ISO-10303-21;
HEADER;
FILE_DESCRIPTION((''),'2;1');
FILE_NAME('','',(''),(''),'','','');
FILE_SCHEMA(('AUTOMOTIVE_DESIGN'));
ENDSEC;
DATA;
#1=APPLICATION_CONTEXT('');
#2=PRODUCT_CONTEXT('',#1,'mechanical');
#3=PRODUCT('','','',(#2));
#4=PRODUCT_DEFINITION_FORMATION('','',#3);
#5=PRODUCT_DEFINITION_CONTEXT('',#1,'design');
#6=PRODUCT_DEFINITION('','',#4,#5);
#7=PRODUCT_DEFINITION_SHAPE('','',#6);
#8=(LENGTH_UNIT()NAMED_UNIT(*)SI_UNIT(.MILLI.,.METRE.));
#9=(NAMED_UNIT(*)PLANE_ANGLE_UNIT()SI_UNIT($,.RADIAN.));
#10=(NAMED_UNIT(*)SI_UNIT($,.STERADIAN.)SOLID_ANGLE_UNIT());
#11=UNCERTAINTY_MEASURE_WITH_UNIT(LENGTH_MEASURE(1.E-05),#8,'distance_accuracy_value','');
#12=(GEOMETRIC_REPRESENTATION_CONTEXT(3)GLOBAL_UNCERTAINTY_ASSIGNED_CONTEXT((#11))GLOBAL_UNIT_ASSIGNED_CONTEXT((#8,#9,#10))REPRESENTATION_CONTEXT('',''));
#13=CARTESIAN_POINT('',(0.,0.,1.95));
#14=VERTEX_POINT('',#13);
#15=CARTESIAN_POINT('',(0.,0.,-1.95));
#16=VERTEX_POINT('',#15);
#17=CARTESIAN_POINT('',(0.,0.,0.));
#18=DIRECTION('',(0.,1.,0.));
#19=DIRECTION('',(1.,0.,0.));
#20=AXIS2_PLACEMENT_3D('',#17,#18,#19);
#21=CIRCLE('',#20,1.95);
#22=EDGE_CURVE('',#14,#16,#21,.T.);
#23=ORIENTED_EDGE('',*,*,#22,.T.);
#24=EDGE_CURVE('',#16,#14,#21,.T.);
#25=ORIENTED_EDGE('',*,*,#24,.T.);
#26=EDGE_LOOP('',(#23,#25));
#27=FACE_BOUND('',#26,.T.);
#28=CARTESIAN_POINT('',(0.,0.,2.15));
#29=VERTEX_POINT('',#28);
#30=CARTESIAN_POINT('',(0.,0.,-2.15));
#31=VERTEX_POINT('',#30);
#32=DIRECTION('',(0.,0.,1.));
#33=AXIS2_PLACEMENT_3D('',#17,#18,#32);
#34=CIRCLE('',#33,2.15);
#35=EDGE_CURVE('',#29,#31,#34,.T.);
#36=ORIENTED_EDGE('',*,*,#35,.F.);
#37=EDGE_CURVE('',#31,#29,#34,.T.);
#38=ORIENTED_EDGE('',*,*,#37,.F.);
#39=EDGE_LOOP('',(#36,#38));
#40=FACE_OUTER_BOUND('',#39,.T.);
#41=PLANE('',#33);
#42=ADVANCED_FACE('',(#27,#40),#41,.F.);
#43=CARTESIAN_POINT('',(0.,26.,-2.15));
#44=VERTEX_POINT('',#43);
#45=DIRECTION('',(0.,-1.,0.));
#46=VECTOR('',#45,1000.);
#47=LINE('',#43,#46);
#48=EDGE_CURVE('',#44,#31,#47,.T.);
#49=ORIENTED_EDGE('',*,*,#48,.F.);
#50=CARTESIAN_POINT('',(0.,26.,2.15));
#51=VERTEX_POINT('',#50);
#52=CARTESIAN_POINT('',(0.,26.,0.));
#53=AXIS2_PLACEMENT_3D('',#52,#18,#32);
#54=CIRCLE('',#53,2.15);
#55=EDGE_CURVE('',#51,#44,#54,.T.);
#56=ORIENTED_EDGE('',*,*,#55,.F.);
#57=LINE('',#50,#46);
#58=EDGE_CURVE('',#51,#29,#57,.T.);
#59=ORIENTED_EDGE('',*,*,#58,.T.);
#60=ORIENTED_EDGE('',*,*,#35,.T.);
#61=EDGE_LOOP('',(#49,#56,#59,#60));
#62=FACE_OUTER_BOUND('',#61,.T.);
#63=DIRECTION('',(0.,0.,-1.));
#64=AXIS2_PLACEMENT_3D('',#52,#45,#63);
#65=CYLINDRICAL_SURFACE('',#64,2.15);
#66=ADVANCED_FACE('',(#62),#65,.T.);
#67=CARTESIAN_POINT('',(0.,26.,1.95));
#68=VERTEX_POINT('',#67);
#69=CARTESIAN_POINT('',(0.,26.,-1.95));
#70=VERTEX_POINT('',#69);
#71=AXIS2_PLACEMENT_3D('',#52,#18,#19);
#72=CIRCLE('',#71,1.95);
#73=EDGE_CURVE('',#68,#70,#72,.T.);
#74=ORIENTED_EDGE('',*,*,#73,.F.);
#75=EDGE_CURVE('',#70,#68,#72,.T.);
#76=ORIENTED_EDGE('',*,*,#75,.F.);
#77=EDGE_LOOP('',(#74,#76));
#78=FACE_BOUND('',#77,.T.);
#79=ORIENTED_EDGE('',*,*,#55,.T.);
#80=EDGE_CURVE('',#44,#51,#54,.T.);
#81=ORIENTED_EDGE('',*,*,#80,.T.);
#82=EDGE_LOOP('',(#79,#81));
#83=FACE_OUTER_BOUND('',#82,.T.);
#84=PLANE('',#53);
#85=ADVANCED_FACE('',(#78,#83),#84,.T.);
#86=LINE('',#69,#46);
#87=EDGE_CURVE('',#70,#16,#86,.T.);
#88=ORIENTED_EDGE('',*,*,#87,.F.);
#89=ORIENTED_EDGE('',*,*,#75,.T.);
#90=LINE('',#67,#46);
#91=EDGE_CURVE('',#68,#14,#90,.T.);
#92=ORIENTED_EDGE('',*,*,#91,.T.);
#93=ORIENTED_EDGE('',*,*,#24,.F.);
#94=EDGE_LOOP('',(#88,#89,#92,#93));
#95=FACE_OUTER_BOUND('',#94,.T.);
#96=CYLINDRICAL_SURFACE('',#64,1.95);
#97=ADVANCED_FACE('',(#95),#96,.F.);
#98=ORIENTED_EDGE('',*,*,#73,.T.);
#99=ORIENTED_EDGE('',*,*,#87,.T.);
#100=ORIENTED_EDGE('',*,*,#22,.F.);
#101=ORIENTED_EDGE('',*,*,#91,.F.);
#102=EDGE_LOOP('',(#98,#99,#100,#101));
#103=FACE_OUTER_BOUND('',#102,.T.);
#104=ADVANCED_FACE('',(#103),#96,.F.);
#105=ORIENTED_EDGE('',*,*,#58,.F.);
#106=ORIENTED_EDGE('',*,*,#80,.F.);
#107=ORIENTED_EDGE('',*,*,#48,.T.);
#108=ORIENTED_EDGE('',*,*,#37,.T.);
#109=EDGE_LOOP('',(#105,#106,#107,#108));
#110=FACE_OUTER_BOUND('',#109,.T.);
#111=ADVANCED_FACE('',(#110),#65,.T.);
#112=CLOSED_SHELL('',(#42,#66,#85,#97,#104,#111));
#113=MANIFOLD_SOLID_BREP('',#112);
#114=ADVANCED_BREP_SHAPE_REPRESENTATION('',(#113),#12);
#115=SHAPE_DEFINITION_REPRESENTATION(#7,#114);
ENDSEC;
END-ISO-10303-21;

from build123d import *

# Parameters (mm, degrees)
SKETCH_1_R      = 2.15
SKETCH_1_R_2    = 1.95
EXTRUDE_1_DEPTH = 26


with BuildPart() as part:
    # 草图1 → 拉伸-薄壁1 (new body)
    with BuildSketch(Plane(origin=(0, 0, 0), x_dir=(1, 0, 0), z_dir=(0, 1, 0))):
        Circle(SKETCH_1_R)
        Circle(SKETCH_1_R_2, mode=Mode.SUBTRACT)
    extrude(amount=EXTRUDE_1_DEPTH)


solid = part.part
